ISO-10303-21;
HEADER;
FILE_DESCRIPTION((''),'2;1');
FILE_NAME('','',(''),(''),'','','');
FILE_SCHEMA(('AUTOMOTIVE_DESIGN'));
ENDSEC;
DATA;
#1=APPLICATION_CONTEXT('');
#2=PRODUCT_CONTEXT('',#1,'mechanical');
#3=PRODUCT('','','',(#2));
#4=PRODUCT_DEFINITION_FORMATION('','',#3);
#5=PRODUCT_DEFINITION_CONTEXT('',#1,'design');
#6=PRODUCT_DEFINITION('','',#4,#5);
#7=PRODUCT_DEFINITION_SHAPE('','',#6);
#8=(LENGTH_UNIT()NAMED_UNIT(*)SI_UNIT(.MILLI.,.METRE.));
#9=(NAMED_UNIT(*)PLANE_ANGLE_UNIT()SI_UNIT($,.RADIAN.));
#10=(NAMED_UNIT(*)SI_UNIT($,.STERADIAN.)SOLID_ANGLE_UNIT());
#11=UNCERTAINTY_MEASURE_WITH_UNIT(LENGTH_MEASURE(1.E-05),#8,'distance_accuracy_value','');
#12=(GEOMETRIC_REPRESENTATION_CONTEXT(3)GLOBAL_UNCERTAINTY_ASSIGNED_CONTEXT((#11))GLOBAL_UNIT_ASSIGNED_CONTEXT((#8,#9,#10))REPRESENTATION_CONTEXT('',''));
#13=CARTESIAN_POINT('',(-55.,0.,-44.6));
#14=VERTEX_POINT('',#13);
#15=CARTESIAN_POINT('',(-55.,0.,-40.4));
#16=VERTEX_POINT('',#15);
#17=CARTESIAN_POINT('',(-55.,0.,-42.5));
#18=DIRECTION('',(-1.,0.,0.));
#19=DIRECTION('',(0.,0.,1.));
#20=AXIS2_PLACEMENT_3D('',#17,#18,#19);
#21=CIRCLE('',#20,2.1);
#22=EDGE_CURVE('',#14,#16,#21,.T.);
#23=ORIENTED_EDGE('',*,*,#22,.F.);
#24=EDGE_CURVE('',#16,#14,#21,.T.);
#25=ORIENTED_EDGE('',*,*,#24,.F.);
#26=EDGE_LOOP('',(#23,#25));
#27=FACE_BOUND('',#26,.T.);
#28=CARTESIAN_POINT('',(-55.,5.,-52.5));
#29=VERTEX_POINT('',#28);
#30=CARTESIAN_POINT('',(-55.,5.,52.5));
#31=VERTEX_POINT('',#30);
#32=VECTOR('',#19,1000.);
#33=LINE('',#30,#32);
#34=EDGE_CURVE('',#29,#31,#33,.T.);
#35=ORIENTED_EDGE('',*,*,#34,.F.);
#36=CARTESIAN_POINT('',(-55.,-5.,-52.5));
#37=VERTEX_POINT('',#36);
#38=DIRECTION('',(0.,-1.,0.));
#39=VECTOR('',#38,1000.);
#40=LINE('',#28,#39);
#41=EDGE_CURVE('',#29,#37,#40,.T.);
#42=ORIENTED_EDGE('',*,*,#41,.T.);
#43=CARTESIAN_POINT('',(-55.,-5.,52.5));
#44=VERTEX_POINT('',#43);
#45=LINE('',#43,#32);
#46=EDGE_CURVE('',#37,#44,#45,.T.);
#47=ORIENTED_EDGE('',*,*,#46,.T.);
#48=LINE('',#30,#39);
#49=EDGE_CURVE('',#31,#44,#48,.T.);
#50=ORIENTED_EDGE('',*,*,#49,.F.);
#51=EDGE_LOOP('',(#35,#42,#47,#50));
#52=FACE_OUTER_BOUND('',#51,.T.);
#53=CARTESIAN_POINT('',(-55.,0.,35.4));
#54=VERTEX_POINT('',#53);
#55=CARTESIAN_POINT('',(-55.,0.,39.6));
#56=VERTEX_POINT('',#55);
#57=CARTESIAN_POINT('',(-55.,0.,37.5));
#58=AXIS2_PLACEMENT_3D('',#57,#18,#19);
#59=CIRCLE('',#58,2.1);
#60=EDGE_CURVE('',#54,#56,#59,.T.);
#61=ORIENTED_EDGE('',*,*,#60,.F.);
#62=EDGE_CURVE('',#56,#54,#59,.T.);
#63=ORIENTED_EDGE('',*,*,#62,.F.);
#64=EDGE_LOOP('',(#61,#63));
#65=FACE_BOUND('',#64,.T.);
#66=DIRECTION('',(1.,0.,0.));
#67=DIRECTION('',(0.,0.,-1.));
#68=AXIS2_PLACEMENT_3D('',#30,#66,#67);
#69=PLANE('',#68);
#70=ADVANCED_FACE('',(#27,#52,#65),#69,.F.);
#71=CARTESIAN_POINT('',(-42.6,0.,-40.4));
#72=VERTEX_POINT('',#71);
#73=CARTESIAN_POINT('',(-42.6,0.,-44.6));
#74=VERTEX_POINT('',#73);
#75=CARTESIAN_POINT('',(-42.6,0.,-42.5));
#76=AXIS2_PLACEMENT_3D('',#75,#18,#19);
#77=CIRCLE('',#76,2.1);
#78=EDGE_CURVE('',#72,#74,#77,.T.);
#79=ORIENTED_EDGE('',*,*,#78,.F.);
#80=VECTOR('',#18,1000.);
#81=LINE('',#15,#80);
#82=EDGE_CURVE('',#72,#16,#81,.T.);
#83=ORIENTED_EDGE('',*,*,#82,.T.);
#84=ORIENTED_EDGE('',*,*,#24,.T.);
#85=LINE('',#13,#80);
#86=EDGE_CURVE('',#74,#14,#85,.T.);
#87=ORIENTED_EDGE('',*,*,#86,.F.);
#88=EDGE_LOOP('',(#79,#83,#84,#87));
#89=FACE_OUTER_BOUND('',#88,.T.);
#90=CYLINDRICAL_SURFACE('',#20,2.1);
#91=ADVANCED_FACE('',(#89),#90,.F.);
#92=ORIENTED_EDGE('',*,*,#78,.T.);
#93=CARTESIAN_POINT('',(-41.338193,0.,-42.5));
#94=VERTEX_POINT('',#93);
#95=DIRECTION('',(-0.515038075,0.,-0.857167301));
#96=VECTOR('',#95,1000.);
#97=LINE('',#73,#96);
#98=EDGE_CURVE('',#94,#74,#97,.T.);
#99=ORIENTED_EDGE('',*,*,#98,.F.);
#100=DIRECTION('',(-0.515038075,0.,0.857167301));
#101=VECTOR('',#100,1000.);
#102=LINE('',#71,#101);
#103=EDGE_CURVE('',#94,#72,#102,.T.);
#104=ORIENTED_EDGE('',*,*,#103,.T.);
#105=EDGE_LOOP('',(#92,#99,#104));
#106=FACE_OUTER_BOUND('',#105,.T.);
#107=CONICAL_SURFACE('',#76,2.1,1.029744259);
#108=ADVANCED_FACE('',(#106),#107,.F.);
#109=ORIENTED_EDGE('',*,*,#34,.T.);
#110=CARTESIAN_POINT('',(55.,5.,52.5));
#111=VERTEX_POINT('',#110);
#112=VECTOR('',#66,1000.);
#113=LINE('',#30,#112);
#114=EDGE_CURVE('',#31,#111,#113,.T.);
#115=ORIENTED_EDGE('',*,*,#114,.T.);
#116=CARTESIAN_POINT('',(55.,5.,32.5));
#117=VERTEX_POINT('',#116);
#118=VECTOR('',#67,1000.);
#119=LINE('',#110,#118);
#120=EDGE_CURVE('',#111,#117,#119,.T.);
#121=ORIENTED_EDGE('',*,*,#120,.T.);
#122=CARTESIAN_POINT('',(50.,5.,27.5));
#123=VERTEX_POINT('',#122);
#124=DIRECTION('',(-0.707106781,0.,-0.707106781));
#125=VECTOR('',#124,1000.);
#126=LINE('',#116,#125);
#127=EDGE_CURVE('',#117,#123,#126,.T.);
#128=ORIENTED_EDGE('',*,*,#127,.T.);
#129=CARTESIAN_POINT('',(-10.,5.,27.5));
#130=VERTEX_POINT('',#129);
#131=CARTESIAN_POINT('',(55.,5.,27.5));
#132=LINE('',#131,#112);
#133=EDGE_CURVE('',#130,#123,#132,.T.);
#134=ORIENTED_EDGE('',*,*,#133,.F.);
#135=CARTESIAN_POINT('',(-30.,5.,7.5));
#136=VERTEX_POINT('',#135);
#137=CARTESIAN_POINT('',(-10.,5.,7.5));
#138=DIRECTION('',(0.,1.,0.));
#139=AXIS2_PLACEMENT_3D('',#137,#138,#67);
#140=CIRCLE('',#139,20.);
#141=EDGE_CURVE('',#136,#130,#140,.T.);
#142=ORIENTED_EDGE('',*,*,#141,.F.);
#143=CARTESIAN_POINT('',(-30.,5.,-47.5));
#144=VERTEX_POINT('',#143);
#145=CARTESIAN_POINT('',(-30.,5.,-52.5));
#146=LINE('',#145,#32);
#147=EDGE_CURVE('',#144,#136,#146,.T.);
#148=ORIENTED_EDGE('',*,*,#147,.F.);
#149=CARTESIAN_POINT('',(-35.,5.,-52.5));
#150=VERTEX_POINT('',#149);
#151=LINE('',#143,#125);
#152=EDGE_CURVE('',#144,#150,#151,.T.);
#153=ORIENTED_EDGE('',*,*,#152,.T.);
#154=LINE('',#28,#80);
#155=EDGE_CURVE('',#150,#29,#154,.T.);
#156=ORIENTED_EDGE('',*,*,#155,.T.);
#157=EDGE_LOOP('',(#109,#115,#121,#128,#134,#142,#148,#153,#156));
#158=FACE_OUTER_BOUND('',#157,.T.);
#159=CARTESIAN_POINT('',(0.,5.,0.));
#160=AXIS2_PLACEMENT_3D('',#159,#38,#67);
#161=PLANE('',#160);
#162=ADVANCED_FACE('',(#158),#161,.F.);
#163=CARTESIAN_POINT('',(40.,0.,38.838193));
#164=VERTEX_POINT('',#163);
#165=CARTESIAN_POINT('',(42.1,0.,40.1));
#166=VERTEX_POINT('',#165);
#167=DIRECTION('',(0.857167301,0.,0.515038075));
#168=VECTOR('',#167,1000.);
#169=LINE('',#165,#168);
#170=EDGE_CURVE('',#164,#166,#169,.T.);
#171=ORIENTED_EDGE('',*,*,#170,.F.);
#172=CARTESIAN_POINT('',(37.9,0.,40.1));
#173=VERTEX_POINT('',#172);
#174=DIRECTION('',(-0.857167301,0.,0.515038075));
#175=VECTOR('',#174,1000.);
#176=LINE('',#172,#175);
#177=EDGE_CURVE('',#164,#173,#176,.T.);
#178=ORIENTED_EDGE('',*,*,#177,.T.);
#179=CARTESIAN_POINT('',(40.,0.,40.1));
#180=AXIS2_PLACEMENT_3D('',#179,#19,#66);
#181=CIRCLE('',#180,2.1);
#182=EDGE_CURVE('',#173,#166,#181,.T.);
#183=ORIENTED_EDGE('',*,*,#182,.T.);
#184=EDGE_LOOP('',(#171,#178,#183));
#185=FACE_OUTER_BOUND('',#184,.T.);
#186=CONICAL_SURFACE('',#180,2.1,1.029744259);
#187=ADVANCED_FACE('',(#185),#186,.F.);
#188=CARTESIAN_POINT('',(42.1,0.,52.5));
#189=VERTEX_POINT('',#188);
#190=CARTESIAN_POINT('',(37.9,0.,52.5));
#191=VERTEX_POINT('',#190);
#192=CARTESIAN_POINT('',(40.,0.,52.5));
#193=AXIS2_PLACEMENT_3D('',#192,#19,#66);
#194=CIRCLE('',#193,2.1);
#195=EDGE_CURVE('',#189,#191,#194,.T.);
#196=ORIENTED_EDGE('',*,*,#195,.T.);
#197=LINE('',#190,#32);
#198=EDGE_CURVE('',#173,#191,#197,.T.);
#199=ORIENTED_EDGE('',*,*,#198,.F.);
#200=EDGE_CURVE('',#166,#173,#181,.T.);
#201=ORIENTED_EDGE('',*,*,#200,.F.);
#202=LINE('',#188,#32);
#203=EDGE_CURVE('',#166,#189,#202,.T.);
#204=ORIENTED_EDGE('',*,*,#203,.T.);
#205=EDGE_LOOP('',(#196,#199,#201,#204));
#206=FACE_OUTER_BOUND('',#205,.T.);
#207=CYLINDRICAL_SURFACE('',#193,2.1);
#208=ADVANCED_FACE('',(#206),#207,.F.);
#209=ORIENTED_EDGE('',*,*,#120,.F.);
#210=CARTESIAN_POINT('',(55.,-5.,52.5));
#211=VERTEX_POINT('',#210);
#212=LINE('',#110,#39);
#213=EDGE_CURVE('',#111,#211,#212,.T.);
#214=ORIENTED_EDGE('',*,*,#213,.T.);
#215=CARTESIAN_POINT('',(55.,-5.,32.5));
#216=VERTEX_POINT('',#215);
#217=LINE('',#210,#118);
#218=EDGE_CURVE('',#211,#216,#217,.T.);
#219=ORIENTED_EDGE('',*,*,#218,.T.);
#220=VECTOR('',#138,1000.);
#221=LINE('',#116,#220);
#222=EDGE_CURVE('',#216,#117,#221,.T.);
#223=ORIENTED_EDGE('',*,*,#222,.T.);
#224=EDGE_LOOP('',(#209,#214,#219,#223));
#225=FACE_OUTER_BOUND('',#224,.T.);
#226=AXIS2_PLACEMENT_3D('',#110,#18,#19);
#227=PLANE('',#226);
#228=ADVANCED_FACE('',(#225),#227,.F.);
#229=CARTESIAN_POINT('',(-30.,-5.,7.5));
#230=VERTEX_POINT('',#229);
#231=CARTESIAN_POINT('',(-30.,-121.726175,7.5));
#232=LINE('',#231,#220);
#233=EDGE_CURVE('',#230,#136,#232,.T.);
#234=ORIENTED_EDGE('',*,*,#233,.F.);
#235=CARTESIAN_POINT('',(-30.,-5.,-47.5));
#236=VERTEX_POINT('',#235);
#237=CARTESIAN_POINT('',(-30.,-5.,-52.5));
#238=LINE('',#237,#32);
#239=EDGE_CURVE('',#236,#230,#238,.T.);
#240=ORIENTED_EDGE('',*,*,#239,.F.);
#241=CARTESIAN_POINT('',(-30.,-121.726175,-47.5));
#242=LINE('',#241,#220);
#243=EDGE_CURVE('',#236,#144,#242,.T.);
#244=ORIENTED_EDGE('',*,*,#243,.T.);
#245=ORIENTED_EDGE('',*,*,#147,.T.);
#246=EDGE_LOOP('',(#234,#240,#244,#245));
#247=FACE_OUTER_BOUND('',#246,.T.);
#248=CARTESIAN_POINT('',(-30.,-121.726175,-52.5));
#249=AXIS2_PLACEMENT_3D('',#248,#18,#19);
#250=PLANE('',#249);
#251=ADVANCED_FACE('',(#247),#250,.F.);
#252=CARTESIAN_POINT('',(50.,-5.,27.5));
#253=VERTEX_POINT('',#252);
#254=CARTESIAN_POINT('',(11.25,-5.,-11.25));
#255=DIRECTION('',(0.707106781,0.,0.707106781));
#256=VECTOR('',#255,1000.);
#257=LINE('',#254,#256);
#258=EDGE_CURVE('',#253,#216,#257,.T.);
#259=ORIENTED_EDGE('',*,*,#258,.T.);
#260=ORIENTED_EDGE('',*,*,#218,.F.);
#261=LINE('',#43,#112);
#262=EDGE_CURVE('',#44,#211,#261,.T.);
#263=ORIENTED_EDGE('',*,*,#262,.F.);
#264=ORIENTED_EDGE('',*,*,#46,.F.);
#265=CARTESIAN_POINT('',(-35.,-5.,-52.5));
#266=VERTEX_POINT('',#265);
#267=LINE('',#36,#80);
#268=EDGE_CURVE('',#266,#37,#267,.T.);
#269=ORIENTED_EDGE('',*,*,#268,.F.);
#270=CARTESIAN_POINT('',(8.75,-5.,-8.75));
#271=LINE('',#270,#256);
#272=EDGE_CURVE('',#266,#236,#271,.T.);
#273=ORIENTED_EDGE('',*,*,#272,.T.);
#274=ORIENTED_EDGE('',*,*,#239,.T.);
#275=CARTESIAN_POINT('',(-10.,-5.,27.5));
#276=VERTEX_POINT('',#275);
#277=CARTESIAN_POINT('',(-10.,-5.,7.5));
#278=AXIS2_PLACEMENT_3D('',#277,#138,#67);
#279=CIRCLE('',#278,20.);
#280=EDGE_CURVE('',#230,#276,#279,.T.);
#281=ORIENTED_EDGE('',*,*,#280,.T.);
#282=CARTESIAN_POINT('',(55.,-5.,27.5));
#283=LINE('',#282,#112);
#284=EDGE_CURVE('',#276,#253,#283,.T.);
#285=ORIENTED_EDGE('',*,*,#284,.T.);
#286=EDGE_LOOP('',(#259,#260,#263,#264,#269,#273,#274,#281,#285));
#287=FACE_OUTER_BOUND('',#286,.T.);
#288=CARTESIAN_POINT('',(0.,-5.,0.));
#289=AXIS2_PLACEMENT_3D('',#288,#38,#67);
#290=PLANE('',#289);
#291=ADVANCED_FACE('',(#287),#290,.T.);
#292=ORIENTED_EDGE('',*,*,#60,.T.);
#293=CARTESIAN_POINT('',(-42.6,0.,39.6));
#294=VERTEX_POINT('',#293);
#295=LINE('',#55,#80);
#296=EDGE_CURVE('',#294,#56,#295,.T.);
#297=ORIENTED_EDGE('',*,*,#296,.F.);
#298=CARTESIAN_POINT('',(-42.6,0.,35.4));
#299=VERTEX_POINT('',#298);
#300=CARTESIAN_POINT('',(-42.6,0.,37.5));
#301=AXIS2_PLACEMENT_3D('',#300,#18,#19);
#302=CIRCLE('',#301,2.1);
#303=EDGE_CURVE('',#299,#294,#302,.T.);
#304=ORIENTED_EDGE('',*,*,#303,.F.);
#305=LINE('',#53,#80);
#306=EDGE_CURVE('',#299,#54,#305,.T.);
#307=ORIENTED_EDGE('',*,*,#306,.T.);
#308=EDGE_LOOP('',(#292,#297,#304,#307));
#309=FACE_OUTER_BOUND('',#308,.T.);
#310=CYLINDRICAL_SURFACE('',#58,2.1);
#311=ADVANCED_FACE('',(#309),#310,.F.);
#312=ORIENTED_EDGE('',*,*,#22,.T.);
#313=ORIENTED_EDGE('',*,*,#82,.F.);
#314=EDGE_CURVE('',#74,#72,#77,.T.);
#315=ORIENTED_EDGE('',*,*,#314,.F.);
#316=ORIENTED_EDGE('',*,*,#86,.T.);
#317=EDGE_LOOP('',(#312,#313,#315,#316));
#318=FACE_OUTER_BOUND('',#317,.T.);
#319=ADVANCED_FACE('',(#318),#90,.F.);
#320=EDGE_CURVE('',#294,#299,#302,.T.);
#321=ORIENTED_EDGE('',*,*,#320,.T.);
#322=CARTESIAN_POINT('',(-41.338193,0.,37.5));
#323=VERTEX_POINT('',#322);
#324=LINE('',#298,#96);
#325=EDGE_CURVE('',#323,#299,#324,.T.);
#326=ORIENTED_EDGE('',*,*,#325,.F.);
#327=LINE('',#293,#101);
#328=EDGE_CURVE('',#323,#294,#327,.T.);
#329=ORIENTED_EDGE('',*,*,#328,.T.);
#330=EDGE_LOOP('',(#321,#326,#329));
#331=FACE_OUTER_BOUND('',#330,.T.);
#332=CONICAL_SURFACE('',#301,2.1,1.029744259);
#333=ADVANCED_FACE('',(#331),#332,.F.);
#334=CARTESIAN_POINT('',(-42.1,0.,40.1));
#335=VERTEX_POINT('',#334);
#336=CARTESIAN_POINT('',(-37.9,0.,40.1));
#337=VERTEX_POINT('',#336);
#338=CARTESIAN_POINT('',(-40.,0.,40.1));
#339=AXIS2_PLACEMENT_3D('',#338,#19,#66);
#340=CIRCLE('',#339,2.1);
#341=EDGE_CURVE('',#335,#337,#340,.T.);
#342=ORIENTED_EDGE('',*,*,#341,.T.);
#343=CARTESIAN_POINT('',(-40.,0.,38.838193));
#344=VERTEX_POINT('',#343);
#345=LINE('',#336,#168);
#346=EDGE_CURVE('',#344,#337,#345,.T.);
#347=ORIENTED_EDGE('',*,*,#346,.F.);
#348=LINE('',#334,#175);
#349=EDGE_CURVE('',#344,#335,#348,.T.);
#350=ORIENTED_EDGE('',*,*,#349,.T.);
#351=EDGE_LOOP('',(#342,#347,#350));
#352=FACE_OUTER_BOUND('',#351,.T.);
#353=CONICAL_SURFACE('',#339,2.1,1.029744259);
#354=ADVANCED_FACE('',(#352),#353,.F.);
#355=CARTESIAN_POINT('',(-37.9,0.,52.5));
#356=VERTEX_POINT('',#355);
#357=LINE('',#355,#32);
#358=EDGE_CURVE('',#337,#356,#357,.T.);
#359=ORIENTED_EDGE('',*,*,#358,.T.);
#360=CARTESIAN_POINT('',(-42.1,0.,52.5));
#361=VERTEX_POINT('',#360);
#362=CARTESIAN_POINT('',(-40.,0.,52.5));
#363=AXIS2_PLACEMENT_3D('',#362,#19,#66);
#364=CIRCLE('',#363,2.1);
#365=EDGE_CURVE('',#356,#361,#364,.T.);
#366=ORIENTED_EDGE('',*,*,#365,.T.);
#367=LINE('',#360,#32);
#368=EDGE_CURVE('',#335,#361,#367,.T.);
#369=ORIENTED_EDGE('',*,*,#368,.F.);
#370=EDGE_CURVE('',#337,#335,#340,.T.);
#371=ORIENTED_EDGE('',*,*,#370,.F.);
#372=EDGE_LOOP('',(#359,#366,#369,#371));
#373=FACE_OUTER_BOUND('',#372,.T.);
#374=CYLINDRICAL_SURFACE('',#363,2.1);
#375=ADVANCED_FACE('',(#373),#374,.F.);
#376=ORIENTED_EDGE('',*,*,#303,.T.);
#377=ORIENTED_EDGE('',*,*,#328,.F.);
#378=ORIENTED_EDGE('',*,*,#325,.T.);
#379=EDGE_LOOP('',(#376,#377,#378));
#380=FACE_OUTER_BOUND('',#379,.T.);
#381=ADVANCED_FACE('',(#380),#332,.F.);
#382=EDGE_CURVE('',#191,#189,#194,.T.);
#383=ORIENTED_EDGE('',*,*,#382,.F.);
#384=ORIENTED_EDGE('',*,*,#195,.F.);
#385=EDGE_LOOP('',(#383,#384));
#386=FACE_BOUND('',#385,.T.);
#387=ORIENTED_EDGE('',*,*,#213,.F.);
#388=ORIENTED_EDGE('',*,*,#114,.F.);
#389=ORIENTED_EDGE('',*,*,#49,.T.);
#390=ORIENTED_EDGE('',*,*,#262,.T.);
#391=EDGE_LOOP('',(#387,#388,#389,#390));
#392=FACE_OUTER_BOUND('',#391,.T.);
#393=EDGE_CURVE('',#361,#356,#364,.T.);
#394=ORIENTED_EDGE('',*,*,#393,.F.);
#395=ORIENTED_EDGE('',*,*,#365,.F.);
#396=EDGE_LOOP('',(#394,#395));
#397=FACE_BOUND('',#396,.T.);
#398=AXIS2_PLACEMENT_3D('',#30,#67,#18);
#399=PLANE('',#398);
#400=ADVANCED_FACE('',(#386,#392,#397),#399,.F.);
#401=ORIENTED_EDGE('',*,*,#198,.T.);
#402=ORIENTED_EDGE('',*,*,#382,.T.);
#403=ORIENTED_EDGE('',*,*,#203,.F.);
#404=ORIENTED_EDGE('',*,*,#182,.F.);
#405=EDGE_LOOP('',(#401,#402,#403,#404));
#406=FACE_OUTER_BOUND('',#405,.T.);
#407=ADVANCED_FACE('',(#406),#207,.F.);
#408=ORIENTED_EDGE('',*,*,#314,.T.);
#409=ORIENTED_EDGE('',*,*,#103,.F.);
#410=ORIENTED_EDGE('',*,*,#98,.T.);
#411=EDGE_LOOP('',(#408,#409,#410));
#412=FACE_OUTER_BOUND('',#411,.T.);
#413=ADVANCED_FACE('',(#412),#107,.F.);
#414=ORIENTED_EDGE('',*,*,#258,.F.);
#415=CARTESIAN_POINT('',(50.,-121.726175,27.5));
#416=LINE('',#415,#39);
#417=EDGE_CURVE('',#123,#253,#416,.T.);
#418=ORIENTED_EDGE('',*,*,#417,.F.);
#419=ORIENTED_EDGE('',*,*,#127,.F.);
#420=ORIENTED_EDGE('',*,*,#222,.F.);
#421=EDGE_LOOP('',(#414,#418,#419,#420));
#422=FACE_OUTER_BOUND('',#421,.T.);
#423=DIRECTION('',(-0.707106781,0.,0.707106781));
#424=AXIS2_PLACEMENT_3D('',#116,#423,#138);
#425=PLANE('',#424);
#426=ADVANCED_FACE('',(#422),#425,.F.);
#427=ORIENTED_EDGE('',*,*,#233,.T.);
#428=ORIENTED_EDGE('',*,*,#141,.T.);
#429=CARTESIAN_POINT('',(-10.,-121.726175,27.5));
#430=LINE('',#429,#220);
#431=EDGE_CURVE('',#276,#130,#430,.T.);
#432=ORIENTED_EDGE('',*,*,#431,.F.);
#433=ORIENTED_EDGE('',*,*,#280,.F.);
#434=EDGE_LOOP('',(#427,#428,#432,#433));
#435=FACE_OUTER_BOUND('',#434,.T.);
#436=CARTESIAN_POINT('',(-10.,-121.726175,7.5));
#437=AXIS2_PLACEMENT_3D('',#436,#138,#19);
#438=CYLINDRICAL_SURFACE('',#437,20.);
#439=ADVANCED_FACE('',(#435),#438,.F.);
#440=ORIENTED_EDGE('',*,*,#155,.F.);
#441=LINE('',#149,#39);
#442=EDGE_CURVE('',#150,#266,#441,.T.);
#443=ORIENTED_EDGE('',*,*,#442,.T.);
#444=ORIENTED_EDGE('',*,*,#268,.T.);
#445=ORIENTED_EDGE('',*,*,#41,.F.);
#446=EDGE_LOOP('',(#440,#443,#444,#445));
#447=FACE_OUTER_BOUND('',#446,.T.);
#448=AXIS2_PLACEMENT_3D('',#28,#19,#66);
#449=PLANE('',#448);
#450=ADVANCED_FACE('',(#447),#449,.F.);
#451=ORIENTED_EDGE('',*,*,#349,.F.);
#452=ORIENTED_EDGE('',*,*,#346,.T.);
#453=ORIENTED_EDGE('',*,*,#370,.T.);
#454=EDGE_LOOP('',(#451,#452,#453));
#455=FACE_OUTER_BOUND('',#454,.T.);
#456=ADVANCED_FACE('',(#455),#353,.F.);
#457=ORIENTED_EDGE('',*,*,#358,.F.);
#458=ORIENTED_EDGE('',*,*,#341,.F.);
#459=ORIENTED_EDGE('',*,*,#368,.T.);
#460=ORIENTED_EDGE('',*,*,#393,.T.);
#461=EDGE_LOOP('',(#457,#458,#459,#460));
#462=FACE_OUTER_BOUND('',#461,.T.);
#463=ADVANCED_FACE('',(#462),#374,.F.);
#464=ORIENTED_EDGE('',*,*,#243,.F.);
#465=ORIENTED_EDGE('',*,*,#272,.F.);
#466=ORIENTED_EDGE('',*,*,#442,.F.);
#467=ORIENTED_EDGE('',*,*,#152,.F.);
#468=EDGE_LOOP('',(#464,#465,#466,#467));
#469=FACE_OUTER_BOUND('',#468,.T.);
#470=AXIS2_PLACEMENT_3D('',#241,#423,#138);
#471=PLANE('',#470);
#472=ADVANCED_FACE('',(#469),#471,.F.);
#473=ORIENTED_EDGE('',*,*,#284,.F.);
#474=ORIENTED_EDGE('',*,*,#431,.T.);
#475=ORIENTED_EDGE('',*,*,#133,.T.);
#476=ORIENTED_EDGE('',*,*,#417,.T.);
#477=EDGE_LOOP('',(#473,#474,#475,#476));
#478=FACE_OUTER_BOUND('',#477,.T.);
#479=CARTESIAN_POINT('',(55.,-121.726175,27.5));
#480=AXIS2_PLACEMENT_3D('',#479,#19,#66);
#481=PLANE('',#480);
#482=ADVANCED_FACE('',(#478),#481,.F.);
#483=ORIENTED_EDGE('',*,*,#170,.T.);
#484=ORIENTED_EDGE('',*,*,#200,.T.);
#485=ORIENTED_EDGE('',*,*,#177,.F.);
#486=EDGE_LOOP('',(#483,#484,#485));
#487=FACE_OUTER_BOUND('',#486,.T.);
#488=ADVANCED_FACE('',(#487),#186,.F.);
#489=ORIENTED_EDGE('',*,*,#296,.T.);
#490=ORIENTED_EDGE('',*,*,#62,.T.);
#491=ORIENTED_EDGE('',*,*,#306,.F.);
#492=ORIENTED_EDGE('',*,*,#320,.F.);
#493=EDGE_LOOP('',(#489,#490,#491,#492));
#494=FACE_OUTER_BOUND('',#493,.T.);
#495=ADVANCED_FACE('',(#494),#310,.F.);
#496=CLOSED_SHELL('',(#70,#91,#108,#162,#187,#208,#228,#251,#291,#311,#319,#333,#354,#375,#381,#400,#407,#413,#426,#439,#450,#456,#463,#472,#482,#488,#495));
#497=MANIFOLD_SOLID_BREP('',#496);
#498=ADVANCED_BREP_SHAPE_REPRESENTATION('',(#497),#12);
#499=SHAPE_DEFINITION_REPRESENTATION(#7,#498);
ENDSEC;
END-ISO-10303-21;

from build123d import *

# Parameters (mm, degrees)
SKETCH_1_W                  = 110
SKETCH_1_H                  = 105
EXTRUDE_1_DEPTH             = 5
CUT_EXTRUDE_1_DEPTH         = 10
CHAMFER_1_SIZE              = 5
HOLE_WIZARD_M5_1_AT_2_COUNT = 2
HOLE_WIZARD_M5_1_AT_2_PITCH = 80


with BuildPart() as part:
    # 草图1 → 凸台-拉伸1 (new, symmetric)
    with BuildSketch(Plane(origin=(0, 0, 0), x_dir=(1, 0, 0), z_dir=(0, 1, 0))):
        Rectangle(SKETCH_1_W, SKETCH_1_H)
    extrude(amount=EXTRUDE_1_DEPTH, both=True)

    # 草图2 → 切除-拉伸1 (cut)
    with BuildSketch(Plane(origin=(0, 5, 0), x_dir=(1, 0, 0), z_dir=(0, 1, 0))):
        with BuildLine():
            Line((55, 52.5), (-30, 52.5))
            Line((-30, 52.5), (-30, -7.5))
            ThreePointArc((-30, -7.5), (-24.142135624, -21.642135624), (-10, -27.5))
            Line((-10, -27.5), (55, -27.5))
            Line((55, -27.5), (55, 52.5))
        make_face()
    extrude(amount=-CUT_EXTRUDE_1_DEPTH, mode=Mode.SUBTRACT)

    # 倒角1
    chamfer_1_edges = [part.edges().sort_by_distance(p)[0] for p in [
        (-30, 0, -52.5),
        (55, 0, 27.5),
    ]]
    chamfer(chamfer_1_edges, length=CHAMFER_1_SIZE)

    # 草图4 → M5 螺纹孔1 (revolve, cut)
    with BuildSketch(Plane(origin=(-55, 0, 37.5), x_dir=(0, 0, 1), z_dir=(0, 1, 0))):
        Polygon((0, 0), (0, 13.6618073), (2.1, 12.4), (2.1, 0), align=None)
    hole_wizard_m5_1 = revolve(axis=Axis((-61.35, 0, 37.5), (1, 0, 0)), mode=Mode.SUBTRACT)

    # M5 螺纹孔1 at 2: M5 螺纹孔1 ×2
    with Locations(*[(0, 0, -i * HOLE_WIZARD_M5_1_AT_2_PITCH) for i in range(1, HOLE_WIZARD_M5_1_AT_2_COUNT)]):
        add(hole_wizard_m5_1, mode=Mode.SUBTRACT)

    # 镜向1: M5 螺纹孔1 across plane
    add(hole_wizard_m5_1.mirror(Plane(origin=(-1.25, 0, -1.25), x_dir=(-0.7071067811865478, 0, 0.7071067811865472), z_dir=(-0.7071067811865475, 0, -0.7071067811865477))), mode=Mode.SUBTRACT)

    # 镜向1 copy 1 sketch → 镜向1 copy 1 (revolve, cut)
    with BuildSketch(Plane(origin=(40, 0, 52.5), x_dir=(-1, 0, 0), z_dir=(0, 1, 0))):
        Polygon((0, 0), (0, -13.6618073), (2.1, -12.4), (2.1, 0), align=None)
    revolve(axis=Axis((40, 0, 58.85), (0, 0, 1)), mode=Mode.SUBTRACT)


solid = part.part
